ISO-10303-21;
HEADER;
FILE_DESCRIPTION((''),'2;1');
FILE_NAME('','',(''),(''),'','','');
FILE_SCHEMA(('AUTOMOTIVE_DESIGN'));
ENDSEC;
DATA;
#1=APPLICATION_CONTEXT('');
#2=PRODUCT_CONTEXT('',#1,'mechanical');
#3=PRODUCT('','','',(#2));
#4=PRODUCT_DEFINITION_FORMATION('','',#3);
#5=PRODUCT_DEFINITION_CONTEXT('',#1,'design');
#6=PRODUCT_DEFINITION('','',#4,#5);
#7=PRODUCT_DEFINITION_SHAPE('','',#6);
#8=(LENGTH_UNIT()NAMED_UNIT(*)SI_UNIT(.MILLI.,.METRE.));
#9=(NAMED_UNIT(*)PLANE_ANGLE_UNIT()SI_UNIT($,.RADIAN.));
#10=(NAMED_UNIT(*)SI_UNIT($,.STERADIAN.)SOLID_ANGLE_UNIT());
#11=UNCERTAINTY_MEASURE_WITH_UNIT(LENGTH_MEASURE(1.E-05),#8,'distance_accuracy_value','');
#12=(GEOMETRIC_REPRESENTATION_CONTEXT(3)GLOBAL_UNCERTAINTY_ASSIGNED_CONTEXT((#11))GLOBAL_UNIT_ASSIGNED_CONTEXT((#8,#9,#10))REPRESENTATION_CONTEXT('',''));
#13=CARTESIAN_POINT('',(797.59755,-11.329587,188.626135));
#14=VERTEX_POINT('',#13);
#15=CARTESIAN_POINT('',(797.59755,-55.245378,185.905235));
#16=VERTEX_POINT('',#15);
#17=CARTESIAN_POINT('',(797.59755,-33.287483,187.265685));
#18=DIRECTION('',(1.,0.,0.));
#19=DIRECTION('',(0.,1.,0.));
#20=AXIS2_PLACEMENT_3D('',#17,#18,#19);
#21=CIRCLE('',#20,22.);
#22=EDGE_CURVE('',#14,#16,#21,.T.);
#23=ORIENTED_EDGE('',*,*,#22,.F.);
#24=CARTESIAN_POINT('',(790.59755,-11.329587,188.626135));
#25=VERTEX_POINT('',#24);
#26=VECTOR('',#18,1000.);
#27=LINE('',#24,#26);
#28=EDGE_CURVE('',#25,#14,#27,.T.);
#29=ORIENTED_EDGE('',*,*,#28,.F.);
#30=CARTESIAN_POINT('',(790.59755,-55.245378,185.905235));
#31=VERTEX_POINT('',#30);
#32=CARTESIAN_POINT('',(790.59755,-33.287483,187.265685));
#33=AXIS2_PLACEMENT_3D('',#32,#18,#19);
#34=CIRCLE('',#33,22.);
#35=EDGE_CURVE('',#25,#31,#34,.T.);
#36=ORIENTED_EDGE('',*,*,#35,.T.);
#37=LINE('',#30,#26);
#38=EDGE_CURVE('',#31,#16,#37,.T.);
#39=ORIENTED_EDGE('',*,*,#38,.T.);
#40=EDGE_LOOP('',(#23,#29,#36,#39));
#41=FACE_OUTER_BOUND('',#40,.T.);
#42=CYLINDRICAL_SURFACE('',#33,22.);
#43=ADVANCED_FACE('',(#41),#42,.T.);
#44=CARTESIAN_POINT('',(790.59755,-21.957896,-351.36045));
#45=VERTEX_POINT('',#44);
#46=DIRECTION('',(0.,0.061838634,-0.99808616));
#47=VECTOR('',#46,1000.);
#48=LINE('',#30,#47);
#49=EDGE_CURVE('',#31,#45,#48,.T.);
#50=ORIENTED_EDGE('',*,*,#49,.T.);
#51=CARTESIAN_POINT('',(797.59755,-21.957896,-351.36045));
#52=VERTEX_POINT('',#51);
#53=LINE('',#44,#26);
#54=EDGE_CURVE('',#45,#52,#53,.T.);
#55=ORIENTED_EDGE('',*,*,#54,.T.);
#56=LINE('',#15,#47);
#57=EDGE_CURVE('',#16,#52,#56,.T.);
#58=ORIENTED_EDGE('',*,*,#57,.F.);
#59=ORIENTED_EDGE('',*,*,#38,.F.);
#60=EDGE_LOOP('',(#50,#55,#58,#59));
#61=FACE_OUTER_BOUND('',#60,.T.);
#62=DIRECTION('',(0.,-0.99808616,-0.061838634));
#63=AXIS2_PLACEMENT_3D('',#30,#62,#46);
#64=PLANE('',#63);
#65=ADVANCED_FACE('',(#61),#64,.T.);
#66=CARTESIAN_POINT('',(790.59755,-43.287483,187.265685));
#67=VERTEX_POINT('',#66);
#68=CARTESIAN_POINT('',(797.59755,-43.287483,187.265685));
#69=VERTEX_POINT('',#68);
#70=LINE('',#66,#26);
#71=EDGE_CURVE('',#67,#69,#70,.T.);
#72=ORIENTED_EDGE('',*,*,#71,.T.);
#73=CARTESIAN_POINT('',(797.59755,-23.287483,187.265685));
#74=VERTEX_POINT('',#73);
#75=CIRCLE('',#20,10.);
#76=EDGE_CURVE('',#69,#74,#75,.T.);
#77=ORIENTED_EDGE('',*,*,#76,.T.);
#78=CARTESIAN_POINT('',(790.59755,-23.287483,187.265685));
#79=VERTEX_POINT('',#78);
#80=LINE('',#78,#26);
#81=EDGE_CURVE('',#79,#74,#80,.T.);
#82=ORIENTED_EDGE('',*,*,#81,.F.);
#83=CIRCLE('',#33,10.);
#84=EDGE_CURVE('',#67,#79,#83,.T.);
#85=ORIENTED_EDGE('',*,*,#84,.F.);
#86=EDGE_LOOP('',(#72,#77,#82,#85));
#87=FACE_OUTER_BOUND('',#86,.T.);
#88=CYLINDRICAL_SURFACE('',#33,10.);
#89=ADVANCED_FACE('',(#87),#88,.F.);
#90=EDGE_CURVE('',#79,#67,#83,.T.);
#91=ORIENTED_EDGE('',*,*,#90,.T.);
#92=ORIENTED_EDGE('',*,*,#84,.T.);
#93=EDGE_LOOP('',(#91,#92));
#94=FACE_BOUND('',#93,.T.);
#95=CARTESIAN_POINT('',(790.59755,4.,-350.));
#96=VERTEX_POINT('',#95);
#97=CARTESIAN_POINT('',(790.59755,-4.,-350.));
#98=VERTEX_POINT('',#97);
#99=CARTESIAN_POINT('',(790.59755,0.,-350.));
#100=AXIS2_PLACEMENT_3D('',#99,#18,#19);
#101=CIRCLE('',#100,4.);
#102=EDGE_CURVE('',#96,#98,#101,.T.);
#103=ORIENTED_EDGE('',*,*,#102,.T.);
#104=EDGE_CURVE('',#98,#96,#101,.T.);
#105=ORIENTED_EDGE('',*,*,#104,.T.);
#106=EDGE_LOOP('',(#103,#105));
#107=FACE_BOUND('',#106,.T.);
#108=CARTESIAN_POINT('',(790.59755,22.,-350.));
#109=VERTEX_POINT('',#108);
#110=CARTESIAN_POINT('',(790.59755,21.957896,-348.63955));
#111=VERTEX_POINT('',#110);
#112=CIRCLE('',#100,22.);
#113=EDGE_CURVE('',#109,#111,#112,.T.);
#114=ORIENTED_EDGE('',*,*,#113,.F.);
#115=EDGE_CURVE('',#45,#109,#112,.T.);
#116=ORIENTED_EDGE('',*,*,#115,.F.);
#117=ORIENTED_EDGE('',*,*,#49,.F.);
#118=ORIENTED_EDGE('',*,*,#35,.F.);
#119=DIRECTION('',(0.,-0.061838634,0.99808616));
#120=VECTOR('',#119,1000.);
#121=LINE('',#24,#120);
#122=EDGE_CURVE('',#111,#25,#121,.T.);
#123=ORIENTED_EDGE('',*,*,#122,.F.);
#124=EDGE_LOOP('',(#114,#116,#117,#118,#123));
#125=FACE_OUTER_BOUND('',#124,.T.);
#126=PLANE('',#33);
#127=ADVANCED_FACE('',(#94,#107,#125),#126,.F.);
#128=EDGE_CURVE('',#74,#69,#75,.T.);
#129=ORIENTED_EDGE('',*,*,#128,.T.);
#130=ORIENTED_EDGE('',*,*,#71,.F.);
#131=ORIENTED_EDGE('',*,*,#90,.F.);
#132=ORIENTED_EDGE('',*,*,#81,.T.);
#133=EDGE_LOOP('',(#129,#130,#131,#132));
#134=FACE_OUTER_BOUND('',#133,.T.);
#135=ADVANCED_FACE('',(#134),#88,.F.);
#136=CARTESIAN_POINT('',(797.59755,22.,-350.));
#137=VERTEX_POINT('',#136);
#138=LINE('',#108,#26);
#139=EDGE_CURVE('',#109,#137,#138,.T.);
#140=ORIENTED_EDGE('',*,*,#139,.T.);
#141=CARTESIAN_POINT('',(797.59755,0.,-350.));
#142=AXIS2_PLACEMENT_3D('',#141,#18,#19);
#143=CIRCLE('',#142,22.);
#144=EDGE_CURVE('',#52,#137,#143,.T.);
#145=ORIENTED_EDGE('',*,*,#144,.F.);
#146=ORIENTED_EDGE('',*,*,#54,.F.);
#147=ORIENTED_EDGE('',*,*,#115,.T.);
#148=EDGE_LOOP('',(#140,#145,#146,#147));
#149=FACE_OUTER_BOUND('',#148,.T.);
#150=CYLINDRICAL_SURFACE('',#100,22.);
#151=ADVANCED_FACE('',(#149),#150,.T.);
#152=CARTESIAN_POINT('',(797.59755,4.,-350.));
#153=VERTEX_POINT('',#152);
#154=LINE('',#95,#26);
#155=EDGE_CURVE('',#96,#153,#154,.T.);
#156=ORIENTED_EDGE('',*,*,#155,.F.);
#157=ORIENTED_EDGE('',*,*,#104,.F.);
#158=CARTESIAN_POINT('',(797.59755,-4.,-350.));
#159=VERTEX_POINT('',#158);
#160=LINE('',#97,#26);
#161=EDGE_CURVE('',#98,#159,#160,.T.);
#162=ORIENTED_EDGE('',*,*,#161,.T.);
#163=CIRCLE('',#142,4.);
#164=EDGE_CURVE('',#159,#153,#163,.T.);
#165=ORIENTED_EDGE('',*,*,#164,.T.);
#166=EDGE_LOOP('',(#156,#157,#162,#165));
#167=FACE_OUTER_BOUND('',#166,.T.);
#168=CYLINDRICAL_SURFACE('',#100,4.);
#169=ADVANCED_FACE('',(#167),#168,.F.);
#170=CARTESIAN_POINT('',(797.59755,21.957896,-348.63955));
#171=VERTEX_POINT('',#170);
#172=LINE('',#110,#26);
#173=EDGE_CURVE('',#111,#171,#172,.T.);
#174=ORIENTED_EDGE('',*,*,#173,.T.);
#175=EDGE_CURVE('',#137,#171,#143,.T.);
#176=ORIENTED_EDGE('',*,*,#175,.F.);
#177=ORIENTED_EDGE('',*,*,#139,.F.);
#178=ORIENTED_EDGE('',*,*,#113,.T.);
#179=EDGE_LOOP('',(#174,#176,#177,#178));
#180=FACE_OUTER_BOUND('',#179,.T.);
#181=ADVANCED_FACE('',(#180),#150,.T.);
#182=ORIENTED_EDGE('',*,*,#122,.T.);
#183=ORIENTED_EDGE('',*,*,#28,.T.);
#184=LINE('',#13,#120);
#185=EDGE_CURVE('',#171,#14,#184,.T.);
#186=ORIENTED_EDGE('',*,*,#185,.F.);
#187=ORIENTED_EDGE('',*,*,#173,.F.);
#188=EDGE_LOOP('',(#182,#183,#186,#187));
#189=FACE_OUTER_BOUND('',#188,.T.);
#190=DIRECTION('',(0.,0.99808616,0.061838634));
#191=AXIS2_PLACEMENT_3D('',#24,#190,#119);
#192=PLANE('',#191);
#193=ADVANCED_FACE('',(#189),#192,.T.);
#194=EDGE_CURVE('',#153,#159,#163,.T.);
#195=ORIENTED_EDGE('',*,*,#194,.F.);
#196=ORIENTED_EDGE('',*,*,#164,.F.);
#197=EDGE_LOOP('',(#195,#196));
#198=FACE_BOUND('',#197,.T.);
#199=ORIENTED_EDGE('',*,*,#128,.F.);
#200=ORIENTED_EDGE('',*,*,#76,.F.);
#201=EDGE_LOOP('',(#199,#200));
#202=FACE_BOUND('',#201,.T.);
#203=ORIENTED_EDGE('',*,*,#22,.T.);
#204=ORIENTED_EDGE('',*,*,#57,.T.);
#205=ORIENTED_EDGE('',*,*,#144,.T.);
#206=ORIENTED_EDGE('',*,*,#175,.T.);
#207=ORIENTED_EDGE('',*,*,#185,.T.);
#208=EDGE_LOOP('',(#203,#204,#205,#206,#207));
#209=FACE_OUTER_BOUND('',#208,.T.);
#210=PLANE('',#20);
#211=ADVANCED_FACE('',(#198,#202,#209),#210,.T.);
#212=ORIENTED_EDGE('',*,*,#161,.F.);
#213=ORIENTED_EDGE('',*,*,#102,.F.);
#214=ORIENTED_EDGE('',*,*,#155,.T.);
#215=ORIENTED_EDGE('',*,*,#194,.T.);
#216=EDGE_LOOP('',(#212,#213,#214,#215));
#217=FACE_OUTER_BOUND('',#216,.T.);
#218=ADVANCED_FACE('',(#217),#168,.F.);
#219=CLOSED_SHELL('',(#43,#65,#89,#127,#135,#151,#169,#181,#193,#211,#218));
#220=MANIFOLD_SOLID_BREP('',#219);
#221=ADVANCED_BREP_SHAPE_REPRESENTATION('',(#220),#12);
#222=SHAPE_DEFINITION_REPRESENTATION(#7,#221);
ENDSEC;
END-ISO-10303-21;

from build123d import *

# Parameters (mm, degrees)
SKETCH_1_R      = 4
SKETCH_1_R_2    = 10
EXTRUDE_1_DEPTH = 7


with BuildPart() as part:
    # 草图1 → 凸台-拉伸1 (new body)
    with BuildSketch(Plane(origin=(797.597549653, 0, 0), x_dir=(0, 0, -1), z_dir=(1, 0, 0))):
        with BuildLine():
            Line((-188.626135314, -11.329587329), (348.639550057, 21.957895527))
            ThreePointArc((348.639550057, 21.957895527), (371.957895527, 1.360449943), (351.360449943, -21.957895527))
            Line((351.360449943, -21.957895527), (-185.905235429, -55.245378382))
            ThreePointArc((-185.905235429, -55.245378382), (-209.223580898, -34.647932798), (-188.626135314, -11.329587329))
        make_face()
        with Locations(Location((350, 0, 0), (0, 0, 90))):
            Circle(SKETCH_1_R, mode=Mode.SUBTRACT)
        with Locations(Location((-187.265685371, -33.287482855, 0), (0, 0, 90))):
            Circle(SKETCH_1_R_2, mode=Mode.SUBTRACT)
    extrude(amount=-EXTRUDE_1_DEPTH)


solid = part.part
